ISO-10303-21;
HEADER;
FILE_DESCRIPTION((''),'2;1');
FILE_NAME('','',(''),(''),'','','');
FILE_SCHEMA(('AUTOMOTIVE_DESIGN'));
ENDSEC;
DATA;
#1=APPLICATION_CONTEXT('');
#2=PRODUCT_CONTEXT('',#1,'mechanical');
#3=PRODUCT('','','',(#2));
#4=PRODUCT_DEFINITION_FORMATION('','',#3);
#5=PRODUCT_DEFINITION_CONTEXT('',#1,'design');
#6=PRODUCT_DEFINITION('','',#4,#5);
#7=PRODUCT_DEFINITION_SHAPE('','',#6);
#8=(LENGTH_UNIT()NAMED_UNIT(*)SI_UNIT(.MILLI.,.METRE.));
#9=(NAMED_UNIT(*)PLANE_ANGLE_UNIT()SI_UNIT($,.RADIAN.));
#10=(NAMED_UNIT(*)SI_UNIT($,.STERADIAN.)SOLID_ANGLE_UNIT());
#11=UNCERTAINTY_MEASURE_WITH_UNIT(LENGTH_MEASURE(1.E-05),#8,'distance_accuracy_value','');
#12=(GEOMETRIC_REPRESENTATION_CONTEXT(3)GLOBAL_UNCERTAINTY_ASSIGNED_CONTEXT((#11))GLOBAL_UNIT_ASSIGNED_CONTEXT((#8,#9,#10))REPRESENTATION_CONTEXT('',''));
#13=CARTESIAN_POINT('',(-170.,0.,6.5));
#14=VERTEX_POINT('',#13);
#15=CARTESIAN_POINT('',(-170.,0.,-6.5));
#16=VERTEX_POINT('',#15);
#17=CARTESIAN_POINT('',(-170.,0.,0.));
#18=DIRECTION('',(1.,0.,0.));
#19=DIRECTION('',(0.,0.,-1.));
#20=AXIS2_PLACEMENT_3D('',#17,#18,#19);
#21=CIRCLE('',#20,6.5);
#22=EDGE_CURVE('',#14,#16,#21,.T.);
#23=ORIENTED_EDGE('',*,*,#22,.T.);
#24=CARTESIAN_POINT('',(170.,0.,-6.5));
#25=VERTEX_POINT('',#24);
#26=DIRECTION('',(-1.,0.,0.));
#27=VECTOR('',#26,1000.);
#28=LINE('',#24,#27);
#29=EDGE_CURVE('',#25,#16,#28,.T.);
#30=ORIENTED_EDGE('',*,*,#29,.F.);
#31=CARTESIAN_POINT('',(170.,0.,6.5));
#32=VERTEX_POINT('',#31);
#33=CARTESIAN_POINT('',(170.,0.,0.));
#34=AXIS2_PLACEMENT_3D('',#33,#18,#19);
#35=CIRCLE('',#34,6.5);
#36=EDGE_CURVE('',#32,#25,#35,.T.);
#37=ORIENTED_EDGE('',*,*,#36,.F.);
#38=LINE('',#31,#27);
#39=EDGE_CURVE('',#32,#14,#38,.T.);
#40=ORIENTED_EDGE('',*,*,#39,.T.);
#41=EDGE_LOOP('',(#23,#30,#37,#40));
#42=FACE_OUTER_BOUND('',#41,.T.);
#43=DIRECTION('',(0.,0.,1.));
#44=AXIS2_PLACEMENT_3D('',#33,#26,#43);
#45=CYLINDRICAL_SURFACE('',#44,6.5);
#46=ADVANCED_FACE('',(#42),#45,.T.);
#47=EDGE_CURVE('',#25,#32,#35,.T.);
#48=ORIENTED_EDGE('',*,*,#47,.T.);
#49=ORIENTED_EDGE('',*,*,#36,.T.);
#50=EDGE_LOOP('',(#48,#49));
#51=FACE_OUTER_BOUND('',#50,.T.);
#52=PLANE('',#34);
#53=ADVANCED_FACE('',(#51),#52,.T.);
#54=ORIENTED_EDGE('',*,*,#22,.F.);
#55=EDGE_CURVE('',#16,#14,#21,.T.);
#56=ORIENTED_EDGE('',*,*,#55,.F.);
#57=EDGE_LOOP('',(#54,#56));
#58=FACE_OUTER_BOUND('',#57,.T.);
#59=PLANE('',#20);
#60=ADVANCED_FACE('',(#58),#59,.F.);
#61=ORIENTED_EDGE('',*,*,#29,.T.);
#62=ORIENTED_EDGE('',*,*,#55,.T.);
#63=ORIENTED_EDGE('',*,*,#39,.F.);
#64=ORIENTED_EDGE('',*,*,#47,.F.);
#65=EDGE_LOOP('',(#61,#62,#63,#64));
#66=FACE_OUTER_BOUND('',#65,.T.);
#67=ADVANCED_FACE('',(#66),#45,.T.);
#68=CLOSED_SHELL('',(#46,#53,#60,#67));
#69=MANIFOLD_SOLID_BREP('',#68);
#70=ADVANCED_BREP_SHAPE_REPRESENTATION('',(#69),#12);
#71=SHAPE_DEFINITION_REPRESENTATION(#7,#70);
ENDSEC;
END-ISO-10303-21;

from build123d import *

# Parameters (mm, degrees)
SKETCH1_R           = 6.5
BOSS_EXTRUDE1_DEPTH = 170


with BuildPart() as part:
    # Sketch1 → Boss-Extrude1 (new, symmetric)
    with BuildSketch(Plane(origin=(0, 0, 0), x_dir=(0, 0, -1), z_dir=(1, 0, 0))):
        Circle(SKETCH1_R)
    extrude(amount=BOSS_EXTRUDE1_DEPTH, both=True)


solid = part.part
